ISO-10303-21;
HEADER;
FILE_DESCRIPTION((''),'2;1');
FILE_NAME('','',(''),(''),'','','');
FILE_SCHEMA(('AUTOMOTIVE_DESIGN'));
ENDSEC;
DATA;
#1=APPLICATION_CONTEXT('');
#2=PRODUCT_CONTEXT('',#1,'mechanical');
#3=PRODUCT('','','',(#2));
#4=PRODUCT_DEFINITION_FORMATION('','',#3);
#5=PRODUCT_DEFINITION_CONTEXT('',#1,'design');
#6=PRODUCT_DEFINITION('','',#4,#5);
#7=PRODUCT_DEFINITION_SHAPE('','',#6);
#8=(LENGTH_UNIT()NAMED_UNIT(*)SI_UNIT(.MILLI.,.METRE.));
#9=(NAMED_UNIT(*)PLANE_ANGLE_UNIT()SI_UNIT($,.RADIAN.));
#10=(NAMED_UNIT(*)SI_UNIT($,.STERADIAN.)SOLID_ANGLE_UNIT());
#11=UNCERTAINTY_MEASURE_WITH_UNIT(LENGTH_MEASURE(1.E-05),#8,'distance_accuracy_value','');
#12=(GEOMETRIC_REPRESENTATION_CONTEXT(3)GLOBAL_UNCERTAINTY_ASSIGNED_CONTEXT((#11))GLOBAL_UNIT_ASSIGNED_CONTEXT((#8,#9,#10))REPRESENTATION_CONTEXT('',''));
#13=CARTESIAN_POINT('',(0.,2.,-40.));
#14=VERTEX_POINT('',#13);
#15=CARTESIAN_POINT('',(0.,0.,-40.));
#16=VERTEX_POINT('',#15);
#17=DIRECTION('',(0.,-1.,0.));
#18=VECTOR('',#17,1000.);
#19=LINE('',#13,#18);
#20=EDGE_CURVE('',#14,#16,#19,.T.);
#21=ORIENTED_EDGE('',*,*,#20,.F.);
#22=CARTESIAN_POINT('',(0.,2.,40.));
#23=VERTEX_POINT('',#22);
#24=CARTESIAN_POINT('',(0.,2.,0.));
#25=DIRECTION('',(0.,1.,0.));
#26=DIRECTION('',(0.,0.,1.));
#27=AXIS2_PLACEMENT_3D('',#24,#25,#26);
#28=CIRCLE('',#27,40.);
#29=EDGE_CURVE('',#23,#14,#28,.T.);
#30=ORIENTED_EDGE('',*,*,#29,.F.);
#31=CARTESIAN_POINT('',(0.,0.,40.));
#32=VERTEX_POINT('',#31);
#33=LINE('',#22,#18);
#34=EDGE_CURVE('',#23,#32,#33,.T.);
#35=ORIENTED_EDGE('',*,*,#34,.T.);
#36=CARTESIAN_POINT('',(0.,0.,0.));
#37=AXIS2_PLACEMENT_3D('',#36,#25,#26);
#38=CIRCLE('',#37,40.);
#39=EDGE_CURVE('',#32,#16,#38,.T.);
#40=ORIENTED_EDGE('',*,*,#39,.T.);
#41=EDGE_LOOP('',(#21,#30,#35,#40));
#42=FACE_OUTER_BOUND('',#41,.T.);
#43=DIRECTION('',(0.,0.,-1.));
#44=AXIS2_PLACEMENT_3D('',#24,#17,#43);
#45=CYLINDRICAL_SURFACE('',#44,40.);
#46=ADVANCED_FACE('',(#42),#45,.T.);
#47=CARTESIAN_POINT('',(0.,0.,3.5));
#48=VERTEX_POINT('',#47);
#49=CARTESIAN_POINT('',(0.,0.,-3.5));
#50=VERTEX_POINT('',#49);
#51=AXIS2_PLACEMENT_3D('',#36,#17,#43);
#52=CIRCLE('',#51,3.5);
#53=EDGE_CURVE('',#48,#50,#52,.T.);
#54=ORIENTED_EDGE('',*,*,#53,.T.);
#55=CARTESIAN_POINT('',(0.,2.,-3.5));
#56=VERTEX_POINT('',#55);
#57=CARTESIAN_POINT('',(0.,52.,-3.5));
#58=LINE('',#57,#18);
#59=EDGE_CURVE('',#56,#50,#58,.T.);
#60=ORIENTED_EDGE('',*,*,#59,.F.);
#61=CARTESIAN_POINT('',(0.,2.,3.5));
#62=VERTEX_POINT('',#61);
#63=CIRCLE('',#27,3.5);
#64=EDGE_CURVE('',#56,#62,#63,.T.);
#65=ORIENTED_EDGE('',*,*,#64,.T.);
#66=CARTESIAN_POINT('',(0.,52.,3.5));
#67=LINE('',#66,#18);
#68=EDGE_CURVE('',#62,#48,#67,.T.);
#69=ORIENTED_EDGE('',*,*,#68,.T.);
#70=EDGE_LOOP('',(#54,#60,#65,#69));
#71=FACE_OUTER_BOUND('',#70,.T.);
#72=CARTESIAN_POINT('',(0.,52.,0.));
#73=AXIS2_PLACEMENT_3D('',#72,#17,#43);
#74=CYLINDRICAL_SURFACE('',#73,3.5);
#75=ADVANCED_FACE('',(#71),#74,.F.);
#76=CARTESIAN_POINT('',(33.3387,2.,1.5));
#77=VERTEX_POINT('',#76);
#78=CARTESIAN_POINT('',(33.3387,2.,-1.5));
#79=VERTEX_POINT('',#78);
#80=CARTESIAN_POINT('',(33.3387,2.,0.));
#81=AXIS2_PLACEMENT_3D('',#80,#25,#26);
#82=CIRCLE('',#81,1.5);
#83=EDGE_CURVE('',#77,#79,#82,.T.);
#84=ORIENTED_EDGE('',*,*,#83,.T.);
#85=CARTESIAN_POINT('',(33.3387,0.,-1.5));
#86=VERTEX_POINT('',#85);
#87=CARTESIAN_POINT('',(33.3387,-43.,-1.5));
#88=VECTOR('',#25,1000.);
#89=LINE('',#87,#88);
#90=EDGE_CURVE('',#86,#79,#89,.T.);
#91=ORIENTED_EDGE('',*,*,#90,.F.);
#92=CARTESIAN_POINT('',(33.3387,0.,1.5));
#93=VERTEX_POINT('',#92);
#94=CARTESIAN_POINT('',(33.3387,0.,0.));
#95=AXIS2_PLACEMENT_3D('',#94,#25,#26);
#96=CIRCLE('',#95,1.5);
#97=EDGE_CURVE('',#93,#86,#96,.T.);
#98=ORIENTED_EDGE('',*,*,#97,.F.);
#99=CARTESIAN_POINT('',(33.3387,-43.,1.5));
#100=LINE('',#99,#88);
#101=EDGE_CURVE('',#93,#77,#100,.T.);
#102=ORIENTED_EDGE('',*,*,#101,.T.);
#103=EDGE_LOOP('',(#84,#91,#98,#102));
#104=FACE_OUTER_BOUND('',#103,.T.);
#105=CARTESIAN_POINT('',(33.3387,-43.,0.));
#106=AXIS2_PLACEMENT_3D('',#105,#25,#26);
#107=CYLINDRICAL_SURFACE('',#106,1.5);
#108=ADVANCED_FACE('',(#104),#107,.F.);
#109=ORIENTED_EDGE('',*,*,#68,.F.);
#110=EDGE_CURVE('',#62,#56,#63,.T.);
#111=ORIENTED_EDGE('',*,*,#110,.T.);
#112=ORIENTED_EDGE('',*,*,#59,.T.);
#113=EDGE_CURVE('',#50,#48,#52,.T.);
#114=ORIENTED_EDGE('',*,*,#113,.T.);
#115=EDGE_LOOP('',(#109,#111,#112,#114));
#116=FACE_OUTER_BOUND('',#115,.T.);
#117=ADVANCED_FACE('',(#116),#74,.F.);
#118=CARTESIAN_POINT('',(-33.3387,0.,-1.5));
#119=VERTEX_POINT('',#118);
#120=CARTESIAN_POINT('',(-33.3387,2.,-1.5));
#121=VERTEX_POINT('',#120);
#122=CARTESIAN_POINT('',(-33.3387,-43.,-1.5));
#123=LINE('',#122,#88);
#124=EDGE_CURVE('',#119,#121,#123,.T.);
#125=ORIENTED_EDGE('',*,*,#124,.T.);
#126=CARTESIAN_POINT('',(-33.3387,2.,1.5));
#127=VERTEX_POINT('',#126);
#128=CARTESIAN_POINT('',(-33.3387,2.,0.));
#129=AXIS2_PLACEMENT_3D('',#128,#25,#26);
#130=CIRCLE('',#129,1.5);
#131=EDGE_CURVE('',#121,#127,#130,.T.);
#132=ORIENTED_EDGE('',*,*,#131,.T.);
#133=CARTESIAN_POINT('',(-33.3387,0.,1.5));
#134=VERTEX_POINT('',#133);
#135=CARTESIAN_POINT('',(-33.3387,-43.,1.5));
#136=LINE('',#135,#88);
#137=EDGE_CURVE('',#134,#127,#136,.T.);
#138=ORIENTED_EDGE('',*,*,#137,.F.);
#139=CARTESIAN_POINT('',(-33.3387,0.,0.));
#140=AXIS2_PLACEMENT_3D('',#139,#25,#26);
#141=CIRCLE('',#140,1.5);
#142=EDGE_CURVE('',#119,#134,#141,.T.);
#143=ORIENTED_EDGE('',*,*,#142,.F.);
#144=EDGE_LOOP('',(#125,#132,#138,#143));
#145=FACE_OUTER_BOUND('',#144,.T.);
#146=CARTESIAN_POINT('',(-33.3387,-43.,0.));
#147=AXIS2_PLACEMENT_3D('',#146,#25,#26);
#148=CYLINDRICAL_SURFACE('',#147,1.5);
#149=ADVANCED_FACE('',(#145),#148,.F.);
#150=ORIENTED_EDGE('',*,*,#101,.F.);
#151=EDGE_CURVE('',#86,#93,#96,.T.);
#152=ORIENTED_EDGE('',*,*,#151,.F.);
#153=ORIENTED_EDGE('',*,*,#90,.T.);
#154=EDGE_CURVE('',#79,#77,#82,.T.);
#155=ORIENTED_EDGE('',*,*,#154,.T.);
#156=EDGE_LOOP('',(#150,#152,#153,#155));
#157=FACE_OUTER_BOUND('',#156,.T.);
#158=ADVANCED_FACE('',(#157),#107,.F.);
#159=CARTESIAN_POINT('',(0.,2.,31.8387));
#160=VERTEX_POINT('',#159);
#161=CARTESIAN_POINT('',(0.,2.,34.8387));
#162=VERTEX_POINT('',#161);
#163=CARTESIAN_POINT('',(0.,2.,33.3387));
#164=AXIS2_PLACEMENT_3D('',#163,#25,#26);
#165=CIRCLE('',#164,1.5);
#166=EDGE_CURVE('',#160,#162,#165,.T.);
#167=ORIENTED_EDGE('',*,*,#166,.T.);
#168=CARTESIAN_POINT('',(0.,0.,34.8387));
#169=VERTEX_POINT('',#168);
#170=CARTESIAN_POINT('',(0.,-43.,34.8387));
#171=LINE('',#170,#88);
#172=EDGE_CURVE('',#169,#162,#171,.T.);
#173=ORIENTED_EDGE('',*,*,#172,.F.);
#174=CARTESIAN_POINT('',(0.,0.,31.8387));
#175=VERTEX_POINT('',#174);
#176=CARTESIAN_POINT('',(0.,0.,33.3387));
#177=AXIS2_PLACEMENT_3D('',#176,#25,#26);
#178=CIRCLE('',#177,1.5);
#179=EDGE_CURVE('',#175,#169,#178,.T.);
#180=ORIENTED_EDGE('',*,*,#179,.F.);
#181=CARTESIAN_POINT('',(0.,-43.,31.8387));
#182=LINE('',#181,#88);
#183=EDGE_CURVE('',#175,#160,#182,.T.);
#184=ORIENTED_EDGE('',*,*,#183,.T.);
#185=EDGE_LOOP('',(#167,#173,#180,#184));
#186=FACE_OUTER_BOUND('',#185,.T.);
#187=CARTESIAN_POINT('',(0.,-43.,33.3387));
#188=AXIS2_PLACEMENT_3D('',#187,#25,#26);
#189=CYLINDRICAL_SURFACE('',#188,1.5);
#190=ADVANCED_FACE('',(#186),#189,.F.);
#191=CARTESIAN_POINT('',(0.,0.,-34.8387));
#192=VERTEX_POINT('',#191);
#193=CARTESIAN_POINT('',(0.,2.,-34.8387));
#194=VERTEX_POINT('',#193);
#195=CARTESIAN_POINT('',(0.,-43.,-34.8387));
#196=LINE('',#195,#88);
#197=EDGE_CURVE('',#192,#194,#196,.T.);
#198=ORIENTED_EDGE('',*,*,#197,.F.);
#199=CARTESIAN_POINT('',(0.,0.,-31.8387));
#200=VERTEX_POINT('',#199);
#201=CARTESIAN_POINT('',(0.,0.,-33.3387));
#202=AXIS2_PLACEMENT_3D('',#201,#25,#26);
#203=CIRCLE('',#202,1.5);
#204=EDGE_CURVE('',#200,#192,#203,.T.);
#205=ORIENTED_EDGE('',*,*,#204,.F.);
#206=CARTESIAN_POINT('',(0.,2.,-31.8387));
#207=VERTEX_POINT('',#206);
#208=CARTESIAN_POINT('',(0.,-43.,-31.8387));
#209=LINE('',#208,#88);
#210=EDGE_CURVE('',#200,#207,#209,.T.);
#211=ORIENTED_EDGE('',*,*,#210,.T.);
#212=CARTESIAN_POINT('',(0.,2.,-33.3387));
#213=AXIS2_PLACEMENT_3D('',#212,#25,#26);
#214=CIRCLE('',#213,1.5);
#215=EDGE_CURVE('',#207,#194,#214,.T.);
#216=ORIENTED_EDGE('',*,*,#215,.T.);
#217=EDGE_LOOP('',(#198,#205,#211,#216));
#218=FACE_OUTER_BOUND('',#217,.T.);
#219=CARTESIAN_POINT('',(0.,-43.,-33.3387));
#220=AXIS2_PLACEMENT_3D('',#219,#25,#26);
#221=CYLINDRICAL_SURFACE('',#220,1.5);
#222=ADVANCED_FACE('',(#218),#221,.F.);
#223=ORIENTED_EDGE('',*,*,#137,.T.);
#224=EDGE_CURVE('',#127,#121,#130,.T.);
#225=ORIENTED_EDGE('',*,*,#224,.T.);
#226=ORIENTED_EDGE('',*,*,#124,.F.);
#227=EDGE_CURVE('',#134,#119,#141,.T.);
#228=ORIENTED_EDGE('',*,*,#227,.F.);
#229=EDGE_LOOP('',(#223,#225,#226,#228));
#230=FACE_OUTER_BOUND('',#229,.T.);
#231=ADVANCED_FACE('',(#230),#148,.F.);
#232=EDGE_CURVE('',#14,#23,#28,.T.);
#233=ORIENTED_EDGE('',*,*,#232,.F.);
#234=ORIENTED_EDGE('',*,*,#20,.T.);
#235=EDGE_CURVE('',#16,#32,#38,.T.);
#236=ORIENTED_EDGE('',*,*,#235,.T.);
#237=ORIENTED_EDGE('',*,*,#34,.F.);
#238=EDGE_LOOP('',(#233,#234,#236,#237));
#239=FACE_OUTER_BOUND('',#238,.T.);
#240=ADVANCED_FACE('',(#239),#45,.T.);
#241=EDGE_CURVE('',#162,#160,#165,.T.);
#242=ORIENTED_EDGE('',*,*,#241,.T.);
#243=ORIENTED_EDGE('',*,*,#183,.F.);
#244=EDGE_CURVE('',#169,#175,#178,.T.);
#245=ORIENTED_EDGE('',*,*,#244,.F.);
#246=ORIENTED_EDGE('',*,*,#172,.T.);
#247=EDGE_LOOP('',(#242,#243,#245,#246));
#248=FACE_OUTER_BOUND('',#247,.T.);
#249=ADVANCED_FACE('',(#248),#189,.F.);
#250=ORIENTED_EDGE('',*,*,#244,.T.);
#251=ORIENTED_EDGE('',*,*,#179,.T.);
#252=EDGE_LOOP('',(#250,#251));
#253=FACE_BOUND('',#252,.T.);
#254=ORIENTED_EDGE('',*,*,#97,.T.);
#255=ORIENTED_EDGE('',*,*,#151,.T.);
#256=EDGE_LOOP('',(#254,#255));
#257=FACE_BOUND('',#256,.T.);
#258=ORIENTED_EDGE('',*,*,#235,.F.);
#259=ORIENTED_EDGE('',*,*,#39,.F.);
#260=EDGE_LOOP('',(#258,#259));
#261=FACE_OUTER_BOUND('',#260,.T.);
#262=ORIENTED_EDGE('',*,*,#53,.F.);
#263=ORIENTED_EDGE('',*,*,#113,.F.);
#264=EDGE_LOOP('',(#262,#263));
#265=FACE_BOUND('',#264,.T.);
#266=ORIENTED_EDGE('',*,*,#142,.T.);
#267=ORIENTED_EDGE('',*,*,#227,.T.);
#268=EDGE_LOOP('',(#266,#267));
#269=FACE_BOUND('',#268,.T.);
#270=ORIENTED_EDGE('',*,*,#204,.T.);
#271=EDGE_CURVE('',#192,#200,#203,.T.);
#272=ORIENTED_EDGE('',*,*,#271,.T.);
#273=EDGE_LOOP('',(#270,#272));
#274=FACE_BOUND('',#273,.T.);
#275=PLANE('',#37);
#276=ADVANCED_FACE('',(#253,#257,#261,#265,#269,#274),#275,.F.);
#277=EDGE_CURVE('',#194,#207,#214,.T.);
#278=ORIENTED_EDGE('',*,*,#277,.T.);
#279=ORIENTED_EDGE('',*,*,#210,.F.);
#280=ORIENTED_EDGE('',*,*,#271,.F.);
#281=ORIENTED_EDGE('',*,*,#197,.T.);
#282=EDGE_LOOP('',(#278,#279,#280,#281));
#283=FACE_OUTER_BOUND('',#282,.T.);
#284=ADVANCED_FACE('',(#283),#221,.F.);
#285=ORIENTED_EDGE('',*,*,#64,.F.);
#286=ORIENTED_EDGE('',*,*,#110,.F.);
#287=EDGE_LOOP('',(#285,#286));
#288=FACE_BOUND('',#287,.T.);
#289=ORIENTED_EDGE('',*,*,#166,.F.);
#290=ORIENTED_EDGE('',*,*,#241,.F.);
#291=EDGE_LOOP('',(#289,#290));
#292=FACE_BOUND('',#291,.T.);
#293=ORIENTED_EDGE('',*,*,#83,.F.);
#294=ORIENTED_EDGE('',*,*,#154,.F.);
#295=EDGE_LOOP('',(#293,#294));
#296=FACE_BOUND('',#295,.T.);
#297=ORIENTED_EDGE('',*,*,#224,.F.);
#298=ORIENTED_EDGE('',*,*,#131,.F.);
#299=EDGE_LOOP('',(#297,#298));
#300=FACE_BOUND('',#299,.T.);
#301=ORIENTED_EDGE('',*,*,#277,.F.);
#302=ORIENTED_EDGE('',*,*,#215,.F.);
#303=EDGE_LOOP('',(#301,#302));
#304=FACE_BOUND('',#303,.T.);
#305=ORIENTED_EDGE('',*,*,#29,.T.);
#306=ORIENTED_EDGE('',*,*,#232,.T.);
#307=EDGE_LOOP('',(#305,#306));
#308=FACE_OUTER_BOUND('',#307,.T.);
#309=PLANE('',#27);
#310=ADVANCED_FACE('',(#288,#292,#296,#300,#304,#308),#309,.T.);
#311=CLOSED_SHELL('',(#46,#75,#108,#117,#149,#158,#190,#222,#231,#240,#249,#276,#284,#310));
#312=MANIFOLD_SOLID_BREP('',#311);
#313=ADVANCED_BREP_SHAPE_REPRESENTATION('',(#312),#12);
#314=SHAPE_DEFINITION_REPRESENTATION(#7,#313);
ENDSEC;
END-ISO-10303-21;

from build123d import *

# Parameters (mm, degrees)
SKETCH1_R           = 40
BOSS_EXTRUDE1_DEPTH = 2
SKETCH2_R           = 3.5
CUT_EXTRUDE3_DEPTH  = 52
SKETCH3_R           = 1.5
CUT_EXTRUDE4_DEPTH  = 45


with BuildPart() as part:
    # Sketch1 → Boss-Extrude1 (new body)
    with BuildSketch(Plane(origin=(0, 0, 0), x_dir=(1, 0, 0), z_dir=(0, 1, 0))):
        with Locations(Location((0, 0, 0), (0, 0, 270))):
            Circle(SKETCH1_R)
    extrude(amount=BOSS_EXTRUDE1_DEPTH)

    # Sketch2 → Cut-Extrude3 (cut)
    with BuildSketch(Plane.XZ):
        with Locations(Location((0, 0, 0), (0, 0, 270))):
            Circle(SKETCH2_R)
    extrude(amount=-CUT_EXTRUDE3_DEPTH, mode=Mode.SUBTRACT)

    # Sketch3 → Cut-Extrude4 (cut)
    with BuildSketch(Plane(origin=(0, 2, 0), x_dir=(1, 0, 0), z_dir=(0, 1, 0))):
        with Locations(Location((0, 33.338700108, 0), (0, 0, 270))):
            Circle(SKETCH3_R)
        with Locations(Location((33.338700108, 0, 0), (0, 0, 270))):
            Circle(SKETCH3_R)
        with Locations(Location((0, -33.338700108, 0), (0, 0, 270))):
            Circle(SKETCH3_R)
        with Locations(Location((-33.338700108, 0, 0), (0, 0, 270))):
            Circle(SKETCH3_R)
    extrude(amount=-CUT_EXTRUDE4_DEPTH, mode=Mode.SUBTRACT)


solid = part.part
